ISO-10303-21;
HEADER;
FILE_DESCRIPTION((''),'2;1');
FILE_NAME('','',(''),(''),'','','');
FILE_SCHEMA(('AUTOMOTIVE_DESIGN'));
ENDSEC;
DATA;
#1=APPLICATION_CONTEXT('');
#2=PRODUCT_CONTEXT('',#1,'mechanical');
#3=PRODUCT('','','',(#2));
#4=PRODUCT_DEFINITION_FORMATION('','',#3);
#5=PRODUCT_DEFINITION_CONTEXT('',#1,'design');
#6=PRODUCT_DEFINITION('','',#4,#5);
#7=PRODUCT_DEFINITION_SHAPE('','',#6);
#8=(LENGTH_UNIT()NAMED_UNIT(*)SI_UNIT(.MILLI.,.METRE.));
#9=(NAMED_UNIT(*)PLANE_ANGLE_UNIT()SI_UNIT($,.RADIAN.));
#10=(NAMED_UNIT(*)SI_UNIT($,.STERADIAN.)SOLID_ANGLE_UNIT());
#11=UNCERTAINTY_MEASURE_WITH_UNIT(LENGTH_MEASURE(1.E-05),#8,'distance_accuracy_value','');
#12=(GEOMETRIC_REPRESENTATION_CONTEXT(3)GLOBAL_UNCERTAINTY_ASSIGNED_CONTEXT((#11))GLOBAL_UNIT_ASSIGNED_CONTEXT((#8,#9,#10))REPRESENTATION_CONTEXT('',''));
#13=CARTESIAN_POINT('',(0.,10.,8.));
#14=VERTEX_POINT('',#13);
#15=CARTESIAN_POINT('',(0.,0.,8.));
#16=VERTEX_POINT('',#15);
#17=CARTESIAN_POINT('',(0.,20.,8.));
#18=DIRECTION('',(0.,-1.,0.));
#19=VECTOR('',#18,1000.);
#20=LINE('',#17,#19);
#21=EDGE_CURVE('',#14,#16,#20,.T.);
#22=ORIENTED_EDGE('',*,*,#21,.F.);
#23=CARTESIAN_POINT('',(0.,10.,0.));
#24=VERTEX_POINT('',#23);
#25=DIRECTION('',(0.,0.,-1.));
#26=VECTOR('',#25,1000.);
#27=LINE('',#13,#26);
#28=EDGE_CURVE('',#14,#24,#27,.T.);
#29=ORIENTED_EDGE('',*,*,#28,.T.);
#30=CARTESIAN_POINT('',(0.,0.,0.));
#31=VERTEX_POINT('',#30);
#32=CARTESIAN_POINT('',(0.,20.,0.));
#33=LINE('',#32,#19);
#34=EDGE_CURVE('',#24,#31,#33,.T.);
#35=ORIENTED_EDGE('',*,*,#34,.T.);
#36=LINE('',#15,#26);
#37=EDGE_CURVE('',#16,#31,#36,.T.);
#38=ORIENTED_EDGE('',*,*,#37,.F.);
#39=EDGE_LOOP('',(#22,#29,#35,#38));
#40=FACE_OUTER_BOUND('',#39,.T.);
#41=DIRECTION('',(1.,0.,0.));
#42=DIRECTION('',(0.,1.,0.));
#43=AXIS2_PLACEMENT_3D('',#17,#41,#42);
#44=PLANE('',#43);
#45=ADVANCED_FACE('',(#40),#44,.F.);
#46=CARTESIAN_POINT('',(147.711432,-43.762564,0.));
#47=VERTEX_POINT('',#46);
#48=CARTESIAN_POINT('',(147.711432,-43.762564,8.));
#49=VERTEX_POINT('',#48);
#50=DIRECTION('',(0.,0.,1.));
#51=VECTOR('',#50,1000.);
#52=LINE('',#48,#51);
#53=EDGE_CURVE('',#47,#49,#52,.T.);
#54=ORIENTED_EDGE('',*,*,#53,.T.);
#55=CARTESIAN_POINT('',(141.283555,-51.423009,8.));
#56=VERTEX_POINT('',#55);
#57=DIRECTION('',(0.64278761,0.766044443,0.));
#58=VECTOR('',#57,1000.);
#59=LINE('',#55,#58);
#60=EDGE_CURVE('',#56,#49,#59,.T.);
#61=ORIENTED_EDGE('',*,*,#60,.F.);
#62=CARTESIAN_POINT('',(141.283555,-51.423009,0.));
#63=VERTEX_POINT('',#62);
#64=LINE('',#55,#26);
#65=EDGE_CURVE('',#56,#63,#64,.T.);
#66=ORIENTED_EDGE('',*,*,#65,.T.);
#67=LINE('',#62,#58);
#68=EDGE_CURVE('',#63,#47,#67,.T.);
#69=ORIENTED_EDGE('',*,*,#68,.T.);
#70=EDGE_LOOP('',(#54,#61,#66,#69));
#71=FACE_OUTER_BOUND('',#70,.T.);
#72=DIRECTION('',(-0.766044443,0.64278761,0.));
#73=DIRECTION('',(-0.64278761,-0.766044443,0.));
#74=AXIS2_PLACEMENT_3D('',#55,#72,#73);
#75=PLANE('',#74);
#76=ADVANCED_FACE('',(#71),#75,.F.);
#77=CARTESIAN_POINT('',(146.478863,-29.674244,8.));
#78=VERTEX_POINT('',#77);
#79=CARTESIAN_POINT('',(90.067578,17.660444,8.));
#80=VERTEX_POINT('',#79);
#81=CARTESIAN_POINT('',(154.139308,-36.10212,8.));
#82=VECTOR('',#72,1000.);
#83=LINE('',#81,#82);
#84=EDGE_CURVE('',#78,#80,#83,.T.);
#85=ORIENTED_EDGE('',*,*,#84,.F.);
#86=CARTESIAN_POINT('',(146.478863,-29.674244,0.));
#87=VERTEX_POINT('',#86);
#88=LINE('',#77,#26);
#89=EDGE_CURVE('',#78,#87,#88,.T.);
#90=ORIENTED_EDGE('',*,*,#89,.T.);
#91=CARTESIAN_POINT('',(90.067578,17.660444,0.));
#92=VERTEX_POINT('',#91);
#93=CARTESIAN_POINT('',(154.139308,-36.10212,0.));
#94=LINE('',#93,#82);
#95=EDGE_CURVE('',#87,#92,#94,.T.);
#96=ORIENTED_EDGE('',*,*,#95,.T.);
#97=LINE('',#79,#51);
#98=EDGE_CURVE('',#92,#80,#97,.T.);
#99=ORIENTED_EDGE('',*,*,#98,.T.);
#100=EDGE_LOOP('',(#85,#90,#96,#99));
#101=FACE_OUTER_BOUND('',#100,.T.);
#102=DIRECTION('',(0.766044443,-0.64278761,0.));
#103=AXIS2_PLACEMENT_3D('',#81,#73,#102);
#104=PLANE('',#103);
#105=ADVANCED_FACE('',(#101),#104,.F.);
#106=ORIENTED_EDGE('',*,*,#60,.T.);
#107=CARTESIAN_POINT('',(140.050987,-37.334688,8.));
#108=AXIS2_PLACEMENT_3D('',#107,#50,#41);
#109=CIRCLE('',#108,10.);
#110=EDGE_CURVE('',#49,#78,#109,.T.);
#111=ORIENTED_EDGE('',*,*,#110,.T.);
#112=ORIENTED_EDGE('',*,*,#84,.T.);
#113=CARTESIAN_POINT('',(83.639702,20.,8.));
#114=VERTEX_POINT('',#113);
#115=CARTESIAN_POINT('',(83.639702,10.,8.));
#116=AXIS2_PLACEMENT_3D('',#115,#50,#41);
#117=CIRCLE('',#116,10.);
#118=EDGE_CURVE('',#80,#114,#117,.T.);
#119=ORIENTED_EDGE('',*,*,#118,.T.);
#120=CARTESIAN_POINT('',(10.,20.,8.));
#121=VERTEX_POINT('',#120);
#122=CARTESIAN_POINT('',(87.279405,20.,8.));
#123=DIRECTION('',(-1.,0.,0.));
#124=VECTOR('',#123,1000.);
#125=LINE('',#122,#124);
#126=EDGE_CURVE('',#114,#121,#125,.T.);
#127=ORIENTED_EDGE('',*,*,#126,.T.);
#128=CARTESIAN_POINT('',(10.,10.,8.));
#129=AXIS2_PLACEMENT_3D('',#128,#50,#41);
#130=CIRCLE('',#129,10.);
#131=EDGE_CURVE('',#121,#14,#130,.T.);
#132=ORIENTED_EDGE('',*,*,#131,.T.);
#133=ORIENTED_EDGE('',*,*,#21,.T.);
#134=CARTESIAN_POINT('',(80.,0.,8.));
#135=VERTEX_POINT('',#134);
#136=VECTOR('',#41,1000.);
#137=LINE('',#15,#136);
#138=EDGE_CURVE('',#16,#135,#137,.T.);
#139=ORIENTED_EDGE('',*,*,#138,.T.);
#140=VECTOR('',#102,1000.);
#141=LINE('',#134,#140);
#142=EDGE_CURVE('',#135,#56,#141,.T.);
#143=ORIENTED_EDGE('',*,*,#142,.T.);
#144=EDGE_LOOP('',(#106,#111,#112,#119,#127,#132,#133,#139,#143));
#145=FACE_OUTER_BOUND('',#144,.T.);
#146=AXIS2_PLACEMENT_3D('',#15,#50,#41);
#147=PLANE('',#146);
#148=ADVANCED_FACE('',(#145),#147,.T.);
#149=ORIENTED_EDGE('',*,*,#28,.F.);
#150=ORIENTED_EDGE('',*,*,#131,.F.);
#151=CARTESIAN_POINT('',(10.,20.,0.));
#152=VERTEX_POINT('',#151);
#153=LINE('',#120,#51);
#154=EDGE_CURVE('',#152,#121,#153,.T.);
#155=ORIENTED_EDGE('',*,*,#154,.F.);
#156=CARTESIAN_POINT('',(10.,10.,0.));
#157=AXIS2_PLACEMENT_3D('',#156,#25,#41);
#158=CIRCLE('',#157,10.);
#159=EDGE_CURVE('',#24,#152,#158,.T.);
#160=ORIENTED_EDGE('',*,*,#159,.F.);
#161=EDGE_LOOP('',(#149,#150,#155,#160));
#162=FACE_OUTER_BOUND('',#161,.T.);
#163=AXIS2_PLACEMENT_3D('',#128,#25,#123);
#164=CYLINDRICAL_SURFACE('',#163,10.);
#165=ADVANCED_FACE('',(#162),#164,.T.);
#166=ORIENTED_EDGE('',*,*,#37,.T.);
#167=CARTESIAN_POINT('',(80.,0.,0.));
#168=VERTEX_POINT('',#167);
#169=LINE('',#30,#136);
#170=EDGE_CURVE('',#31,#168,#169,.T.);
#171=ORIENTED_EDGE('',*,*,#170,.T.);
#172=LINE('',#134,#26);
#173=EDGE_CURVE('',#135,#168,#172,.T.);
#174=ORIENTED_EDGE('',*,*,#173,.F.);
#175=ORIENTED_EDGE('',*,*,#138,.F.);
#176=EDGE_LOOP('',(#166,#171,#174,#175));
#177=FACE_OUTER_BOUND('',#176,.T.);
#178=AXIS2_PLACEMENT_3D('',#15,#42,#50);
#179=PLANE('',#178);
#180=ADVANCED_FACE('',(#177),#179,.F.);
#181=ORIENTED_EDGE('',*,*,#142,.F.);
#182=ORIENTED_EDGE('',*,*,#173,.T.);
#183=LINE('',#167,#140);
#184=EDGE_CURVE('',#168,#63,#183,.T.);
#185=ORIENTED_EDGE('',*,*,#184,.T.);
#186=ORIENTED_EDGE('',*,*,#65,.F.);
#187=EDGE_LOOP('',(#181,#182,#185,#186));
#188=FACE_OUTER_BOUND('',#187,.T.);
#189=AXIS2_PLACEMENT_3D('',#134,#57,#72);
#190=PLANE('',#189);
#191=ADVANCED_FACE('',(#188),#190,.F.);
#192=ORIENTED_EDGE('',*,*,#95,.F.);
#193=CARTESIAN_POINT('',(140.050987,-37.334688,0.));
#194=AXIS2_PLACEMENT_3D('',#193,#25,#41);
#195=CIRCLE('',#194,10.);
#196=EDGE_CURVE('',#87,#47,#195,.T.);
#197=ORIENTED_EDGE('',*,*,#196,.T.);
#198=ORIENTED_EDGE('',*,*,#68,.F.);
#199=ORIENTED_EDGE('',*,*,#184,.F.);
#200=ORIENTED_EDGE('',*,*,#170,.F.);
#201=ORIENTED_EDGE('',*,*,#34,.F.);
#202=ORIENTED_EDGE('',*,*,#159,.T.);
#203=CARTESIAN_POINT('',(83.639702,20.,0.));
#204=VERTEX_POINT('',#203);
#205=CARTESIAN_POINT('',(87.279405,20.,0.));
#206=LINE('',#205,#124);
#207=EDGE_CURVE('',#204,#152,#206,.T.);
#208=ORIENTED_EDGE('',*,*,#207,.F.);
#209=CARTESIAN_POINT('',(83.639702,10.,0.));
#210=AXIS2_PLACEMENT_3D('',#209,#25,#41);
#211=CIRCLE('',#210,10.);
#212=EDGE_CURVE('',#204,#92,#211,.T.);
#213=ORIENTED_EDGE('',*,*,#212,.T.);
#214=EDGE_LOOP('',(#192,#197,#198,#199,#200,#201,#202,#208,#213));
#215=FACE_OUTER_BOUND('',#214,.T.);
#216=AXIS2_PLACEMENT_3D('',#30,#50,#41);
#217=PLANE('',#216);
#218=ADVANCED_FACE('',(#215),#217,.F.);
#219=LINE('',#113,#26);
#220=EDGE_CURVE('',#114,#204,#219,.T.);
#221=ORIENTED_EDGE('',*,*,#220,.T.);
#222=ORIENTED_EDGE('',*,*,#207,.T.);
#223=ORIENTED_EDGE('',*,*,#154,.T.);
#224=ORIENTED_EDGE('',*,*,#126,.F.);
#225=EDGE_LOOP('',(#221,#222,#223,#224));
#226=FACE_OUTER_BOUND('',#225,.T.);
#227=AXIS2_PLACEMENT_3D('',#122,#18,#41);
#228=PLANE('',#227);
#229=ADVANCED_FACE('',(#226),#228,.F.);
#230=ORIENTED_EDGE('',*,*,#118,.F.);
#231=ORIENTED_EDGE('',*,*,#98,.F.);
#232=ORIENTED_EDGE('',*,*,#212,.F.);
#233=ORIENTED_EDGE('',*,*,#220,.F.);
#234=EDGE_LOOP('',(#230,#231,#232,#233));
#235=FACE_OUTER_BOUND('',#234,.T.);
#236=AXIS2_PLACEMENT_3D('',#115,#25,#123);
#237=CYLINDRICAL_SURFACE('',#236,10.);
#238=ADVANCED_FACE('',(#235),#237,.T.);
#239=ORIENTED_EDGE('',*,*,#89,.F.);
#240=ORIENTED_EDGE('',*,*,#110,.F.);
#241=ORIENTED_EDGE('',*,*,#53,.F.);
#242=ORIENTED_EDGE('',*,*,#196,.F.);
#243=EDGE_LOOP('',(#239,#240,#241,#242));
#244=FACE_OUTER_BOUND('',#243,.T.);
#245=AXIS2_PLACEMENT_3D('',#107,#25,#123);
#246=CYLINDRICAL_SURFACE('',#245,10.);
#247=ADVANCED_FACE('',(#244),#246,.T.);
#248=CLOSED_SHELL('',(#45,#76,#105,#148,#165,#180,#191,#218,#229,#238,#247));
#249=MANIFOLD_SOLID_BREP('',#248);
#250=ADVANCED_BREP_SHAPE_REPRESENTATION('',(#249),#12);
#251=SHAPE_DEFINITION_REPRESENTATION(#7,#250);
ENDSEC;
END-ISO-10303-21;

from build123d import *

# Parameters (mm, degrees)
BOSS_EXTRUDE1_DEPTH = 8
FILLET1_R           = 10


with BuildPart() as part:
    # Sketch1 → Boss-Extrude1 (new body)
    with BuildSketch(Plane.XY):
        Polygon((0, 0), (80, 0), (141.28355545, -51.423008775), (154.139307643, -36.102119913), (87.279404685, 20), (0, 20), align=None)
    extrude(amount=BOSS_EXTRUDE1_DEPTH)

    # Fillet1
    fillet1_edges = [part.edges().sort_by_distance(p)[0] for p in [
        (0, 20, 4),
        (87.279404685, 20, 4),
        (154.139307643, -36.102119913, 4),
    ]]
    fillet(fillet1_edges, radius=FILLET1_R)


solid = part.part
